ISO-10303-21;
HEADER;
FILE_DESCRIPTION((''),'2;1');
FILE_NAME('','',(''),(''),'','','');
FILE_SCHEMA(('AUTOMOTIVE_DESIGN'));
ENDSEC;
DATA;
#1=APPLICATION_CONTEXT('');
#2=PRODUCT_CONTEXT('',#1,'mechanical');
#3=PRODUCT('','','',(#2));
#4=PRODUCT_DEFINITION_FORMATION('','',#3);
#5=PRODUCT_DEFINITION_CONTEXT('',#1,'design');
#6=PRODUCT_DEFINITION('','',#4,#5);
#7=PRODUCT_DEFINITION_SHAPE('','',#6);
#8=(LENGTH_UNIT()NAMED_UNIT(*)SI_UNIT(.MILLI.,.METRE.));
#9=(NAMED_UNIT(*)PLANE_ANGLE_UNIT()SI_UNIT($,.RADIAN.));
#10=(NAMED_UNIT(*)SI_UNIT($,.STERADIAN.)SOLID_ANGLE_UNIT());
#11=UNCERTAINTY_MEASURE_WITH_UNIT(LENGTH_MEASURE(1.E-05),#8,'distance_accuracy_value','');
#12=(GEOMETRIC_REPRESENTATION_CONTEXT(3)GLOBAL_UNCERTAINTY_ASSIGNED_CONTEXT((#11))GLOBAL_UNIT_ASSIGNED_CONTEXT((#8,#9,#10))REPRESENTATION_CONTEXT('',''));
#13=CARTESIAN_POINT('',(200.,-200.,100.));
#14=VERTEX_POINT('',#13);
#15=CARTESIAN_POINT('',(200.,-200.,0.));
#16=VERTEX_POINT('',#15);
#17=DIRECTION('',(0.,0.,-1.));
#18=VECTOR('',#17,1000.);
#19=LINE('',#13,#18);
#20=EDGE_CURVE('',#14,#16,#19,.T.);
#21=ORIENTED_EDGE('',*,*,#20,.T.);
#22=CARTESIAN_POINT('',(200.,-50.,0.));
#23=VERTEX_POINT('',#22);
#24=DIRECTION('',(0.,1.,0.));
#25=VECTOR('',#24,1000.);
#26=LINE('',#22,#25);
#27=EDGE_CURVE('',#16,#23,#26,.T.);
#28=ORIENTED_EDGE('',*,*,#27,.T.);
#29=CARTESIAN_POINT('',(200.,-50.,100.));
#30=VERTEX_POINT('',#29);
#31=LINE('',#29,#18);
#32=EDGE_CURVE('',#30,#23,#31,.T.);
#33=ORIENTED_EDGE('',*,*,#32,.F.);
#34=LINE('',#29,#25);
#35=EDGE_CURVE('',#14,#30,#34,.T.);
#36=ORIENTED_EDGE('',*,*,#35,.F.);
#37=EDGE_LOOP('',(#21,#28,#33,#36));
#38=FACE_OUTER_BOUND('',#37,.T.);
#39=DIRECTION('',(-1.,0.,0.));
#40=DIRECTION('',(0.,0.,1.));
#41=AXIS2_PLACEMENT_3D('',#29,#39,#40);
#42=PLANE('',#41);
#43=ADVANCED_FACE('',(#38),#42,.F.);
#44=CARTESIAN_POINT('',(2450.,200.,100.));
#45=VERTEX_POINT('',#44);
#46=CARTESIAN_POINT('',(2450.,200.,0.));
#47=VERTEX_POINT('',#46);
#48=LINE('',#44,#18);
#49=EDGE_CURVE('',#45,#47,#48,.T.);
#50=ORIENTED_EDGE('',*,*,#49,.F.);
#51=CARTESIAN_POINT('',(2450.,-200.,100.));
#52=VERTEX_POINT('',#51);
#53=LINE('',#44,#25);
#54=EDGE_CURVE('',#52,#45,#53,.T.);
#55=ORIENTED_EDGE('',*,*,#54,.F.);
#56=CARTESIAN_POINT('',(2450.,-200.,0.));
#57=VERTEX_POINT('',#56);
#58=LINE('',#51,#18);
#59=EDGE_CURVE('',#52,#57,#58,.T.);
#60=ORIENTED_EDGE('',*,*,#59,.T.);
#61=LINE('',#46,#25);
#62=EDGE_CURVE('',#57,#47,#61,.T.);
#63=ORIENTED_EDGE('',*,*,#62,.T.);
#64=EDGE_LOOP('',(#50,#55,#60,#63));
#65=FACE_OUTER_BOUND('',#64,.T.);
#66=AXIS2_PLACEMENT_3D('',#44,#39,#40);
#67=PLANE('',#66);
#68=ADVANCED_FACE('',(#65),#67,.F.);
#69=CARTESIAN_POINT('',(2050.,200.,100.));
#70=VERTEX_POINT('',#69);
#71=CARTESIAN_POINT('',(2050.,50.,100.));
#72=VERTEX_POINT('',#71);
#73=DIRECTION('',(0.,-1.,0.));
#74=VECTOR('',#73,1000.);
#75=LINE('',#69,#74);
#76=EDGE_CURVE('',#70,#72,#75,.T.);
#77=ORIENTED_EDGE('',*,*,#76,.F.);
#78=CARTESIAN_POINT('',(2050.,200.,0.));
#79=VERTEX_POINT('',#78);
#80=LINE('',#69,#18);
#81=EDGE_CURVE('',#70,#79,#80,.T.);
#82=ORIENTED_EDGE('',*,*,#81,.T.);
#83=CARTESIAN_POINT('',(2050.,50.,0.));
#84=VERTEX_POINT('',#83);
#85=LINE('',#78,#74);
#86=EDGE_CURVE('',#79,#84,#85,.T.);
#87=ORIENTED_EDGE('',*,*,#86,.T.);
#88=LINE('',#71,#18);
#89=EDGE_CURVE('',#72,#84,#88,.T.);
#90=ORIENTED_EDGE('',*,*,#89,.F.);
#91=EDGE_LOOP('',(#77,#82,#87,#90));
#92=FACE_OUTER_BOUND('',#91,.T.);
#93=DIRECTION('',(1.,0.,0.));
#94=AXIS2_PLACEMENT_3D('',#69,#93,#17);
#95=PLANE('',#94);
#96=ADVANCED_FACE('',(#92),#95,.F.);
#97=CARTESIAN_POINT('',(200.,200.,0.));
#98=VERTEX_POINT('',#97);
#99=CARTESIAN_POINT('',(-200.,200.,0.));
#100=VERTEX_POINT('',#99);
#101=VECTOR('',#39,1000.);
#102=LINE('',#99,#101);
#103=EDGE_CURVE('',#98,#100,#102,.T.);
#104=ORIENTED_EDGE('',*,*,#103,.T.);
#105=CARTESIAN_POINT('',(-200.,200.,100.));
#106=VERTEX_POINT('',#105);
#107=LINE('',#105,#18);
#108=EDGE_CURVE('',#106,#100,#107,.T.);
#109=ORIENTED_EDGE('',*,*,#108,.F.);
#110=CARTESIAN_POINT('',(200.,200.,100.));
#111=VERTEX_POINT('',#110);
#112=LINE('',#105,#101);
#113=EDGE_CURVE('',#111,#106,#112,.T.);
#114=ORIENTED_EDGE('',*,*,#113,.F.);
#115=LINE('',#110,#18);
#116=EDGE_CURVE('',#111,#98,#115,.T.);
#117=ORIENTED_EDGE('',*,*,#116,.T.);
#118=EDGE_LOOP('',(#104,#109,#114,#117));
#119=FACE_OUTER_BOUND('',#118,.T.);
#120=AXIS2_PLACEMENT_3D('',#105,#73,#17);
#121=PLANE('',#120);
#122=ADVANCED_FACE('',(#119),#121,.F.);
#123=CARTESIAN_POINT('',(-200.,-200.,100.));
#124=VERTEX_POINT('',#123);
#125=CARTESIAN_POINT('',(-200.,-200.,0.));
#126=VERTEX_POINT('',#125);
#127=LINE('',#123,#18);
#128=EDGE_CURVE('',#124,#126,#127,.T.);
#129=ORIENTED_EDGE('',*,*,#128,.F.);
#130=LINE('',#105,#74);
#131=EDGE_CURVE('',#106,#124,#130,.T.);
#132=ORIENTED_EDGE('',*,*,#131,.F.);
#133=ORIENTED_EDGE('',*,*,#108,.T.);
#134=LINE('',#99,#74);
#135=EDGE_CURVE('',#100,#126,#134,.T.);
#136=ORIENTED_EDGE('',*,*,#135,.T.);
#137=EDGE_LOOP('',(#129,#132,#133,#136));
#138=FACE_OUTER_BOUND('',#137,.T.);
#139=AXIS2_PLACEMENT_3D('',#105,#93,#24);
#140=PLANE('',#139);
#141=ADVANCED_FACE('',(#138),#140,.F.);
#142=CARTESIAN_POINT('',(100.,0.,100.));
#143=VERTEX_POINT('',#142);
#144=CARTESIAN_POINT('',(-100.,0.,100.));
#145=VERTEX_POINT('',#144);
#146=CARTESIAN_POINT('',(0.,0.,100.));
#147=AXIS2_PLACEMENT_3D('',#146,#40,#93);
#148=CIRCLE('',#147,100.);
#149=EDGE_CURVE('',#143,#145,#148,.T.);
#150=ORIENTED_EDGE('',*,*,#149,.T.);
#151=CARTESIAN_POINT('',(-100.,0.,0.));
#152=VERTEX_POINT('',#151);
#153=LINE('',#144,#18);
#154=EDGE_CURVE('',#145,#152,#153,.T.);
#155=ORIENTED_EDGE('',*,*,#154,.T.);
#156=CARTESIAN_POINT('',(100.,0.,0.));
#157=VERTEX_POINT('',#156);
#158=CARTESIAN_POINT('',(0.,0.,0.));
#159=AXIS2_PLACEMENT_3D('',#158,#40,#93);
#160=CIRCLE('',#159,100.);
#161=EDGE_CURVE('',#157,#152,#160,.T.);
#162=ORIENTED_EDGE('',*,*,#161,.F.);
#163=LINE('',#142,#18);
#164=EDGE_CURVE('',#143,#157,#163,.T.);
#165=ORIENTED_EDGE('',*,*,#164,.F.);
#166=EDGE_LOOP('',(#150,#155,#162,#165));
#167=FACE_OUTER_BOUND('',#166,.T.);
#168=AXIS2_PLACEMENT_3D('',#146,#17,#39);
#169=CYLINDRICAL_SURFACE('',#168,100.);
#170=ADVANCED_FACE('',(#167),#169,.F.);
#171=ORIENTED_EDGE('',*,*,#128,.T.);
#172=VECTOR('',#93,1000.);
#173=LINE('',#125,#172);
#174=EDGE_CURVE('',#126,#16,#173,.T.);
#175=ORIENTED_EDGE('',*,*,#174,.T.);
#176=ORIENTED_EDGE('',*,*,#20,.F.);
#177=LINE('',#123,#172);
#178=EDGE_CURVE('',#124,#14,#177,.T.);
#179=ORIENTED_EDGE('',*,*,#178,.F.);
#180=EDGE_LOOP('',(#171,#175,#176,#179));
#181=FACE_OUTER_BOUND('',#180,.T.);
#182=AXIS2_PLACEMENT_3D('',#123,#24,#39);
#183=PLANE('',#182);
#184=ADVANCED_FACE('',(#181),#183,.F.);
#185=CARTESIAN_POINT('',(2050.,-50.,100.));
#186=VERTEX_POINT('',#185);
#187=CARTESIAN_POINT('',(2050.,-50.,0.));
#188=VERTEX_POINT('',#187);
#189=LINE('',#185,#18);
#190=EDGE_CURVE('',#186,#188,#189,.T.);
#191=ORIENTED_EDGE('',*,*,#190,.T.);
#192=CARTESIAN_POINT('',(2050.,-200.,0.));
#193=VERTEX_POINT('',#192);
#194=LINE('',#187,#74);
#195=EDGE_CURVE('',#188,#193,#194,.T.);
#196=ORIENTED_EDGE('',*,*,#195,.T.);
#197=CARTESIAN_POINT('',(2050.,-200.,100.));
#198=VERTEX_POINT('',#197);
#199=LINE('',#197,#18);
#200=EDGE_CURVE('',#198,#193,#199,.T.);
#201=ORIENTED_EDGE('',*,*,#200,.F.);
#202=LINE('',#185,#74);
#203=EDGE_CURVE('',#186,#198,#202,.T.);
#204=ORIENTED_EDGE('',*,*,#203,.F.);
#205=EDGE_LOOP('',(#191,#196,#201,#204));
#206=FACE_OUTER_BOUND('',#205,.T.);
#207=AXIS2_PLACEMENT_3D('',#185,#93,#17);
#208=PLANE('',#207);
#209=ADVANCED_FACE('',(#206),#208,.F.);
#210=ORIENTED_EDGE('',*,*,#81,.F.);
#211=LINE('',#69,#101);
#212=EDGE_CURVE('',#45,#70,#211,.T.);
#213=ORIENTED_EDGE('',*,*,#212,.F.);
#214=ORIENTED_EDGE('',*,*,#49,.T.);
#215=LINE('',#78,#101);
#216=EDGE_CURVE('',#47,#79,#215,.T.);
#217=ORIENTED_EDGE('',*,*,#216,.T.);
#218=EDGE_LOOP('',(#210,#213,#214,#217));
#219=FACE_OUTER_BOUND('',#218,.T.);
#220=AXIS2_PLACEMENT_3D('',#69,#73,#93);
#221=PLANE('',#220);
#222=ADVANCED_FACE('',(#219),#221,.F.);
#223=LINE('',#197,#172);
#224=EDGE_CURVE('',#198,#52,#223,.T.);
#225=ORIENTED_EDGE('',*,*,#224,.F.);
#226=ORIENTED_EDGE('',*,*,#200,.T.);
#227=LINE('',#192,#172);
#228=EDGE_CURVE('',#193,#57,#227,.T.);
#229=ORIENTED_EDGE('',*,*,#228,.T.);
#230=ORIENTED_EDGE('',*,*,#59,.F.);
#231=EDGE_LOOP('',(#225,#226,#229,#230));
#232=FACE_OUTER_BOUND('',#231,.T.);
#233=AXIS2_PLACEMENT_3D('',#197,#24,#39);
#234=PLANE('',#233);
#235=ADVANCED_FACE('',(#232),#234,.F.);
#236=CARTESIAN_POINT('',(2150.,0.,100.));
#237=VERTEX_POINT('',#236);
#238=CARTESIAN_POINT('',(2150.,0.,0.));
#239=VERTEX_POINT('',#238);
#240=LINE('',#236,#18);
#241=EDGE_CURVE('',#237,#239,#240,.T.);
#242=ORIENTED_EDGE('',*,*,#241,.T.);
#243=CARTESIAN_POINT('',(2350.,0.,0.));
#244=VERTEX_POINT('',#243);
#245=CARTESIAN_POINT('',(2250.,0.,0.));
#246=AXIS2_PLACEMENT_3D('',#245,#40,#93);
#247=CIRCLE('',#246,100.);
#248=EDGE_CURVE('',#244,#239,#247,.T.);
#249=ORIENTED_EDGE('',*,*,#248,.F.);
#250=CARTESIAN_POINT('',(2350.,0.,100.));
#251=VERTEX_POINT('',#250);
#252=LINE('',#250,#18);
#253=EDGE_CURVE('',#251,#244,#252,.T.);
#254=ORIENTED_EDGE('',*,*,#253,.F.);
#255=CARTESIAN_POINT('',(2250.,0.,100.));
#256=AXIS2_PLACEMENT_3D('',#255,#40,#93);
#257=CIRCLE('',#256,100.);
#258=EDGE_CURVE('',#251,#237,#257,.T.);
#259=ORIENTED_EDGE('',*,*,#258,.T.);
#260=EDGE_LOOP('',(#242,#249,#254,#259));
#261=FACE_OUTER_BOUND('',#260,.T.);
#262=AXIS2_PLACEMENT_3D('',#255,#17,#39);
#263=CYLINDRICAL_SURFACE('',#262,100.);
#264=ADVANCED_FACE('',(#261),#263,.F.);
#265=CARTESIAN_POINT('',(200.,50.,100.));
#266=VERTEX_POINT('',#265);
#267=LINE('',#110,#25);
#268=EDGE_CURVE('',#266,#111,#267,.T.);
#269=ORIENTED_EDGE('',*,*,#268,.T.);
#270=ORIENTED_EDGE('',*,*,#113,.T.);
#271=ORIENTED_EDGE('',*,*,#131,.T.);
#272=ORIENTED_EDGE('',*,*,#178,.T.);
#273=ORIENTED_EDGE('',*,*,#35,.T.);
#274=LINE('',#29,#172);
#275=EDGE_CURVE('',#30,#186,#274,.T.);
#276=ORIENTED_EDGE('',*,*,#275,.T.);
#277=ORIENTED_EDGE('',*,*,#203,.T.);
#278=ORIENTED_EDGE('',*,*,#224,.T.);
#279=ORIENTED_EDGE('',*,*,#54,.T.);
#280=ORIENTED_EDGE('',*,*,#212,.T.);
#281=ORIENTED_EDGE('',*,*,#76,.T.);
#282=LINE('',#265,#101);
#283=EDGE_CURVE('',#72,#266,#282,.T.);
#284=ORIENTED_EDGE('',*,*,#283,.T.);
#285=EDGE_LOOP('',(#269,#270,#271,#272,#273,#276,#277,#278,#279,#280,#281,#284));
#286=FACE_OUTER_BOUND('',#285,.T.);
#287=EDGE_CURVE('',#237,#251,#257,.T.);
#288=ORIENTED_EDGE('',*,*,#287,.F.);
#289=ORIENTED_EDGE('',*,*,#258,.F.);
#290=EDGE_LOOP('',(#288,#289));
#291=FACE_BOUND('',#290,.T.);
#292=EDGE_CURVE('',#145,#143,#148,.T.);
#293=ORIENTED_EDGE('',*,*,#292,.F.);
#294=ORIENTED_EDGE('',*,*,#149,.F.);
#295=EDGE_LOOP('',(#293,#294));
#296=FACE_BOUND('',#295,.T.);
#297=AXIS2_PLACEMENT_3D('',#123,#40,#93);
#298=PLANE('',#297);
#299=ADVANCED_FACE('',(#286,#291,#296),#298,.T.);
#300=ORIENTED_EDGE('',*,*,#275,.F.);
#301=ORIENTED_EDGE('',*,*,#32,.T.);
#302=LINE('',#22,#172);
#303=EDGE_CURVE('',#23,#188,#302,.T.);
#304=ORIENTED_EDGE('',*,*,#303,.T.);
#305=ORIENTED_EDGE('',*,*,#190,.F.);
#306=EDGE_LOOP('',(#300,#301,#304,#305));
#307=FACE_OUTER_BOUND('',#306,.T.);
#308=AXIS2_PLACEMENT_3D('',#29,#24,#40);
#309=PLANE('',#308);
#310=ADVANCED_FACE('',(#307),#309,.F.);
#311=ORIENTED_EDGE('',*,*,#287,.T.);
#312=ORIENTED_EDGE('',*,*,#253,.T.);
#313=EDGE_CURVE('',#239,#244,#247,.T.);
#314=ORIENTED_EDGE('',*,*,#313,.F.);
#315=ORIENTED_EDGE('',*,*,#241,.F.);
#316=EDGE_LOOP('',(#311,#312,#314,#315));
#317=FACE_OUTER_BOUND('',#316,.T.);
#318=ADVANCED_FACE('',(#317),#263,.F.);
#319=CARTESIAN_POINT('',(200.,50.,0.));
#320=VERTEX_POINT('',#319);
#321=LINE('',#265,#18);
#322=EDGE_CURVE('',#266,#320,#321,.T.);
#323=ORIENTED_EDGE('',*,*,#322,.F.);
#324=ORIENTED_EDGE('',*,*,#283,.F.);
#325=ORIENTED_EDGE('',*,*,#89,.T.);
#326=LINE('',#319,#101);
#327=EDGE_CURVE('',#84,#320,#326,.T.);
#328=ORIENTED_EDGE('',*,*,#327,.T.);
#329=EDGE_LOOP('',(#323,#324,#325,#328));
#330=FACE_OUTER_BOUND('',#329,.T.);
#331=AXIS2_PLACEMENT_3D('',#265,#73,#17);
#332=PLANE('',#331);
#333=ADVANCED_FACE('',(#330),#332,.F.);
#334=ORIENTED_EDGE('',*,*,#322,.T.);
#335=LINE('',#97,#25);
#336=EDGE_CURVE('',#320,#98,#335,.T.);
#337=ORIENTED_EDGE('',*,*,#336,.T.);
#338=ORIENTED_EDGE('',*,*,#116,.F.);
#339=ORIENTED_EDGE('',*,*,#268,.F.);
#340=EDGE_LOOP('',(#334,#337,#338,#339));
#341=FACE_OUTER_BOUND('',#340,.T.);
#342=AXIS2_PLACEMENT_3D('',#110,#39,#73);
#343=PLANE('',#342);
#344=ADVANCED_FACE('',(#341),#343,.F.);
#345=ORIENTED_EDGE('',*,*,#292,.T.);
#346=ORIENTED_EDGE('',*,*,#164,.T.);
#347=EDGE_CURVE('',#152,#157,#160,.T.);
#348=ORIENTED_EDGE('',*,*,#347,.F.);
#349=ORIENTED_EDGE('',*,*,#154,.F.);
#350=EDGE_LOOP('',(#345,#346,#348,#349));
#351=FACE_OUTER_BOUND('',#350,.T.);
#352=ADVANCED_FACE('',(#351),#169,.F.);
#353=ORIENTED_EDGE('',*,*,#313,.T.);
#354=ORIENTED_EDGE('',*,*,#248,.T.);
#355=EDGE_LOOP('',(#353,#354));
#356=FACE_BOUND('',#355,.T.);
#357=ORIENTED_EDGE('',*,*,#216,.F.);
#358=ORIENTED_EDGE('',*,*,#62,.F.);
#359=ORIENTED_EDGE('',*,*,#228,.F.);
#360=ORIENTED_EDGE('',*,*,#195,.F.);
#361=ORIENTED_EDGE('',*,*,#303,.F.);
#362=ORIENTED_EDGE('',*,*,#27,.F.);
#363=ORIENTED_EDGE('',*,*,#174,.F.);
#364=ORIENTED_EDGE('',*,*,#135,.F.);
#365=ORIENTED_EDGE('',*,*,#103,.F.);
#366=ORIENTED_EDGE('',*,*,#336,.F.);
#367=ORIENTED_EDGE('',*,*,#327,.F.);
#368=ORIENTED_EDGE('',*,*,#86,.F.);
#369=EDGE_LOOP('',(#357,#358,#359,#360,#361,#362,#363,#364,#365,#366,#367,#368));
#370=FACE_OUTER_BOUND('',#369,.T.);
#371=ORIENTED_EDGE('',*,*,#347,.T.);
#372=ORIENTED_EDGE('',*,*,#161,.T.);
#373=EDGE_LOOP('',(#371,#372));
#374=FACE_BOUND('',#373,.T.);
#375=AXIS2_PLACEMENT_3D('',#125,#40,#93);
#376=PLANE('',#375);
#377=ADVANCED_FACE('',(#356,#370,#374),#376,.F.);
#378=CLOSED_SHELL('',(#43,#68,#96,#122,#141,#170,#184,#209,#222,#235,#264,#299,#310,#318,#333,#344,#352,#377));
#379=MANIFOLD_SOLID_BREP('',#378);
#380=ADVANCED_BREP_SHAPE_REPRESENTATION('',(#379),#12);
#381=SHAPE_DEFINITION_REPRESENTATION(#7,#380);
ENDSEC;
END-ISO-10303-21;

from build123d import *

# Parameters (mm, degrees)
SKETCH1_R           = 100
BOSS_EXTRUDE1_DEPTH = 100


with BuildPart() as part:
    # Sketch1 → Boss-Extrude1 (new body)
    with BuildSketch(Plane.XY):
        Polygon((200, 50), (2050, 50), (2050, 200), (2450, 200), (2450, -200), (2050, -200), (2050, -50), (200, -50), (200, -200), (-200, -200), (-200, 200), (200, 200), align=None)
        Circle(SKETCH1_R, mode=Mode.SUBTRACT)
        with Locations((2250, 0)):
            Circle(SKETCH1_R, mode=Mode.SUBTRACT)
    extrude(amount=BOSS_EXTRUDE1_DEPTH)


solid = part.part
